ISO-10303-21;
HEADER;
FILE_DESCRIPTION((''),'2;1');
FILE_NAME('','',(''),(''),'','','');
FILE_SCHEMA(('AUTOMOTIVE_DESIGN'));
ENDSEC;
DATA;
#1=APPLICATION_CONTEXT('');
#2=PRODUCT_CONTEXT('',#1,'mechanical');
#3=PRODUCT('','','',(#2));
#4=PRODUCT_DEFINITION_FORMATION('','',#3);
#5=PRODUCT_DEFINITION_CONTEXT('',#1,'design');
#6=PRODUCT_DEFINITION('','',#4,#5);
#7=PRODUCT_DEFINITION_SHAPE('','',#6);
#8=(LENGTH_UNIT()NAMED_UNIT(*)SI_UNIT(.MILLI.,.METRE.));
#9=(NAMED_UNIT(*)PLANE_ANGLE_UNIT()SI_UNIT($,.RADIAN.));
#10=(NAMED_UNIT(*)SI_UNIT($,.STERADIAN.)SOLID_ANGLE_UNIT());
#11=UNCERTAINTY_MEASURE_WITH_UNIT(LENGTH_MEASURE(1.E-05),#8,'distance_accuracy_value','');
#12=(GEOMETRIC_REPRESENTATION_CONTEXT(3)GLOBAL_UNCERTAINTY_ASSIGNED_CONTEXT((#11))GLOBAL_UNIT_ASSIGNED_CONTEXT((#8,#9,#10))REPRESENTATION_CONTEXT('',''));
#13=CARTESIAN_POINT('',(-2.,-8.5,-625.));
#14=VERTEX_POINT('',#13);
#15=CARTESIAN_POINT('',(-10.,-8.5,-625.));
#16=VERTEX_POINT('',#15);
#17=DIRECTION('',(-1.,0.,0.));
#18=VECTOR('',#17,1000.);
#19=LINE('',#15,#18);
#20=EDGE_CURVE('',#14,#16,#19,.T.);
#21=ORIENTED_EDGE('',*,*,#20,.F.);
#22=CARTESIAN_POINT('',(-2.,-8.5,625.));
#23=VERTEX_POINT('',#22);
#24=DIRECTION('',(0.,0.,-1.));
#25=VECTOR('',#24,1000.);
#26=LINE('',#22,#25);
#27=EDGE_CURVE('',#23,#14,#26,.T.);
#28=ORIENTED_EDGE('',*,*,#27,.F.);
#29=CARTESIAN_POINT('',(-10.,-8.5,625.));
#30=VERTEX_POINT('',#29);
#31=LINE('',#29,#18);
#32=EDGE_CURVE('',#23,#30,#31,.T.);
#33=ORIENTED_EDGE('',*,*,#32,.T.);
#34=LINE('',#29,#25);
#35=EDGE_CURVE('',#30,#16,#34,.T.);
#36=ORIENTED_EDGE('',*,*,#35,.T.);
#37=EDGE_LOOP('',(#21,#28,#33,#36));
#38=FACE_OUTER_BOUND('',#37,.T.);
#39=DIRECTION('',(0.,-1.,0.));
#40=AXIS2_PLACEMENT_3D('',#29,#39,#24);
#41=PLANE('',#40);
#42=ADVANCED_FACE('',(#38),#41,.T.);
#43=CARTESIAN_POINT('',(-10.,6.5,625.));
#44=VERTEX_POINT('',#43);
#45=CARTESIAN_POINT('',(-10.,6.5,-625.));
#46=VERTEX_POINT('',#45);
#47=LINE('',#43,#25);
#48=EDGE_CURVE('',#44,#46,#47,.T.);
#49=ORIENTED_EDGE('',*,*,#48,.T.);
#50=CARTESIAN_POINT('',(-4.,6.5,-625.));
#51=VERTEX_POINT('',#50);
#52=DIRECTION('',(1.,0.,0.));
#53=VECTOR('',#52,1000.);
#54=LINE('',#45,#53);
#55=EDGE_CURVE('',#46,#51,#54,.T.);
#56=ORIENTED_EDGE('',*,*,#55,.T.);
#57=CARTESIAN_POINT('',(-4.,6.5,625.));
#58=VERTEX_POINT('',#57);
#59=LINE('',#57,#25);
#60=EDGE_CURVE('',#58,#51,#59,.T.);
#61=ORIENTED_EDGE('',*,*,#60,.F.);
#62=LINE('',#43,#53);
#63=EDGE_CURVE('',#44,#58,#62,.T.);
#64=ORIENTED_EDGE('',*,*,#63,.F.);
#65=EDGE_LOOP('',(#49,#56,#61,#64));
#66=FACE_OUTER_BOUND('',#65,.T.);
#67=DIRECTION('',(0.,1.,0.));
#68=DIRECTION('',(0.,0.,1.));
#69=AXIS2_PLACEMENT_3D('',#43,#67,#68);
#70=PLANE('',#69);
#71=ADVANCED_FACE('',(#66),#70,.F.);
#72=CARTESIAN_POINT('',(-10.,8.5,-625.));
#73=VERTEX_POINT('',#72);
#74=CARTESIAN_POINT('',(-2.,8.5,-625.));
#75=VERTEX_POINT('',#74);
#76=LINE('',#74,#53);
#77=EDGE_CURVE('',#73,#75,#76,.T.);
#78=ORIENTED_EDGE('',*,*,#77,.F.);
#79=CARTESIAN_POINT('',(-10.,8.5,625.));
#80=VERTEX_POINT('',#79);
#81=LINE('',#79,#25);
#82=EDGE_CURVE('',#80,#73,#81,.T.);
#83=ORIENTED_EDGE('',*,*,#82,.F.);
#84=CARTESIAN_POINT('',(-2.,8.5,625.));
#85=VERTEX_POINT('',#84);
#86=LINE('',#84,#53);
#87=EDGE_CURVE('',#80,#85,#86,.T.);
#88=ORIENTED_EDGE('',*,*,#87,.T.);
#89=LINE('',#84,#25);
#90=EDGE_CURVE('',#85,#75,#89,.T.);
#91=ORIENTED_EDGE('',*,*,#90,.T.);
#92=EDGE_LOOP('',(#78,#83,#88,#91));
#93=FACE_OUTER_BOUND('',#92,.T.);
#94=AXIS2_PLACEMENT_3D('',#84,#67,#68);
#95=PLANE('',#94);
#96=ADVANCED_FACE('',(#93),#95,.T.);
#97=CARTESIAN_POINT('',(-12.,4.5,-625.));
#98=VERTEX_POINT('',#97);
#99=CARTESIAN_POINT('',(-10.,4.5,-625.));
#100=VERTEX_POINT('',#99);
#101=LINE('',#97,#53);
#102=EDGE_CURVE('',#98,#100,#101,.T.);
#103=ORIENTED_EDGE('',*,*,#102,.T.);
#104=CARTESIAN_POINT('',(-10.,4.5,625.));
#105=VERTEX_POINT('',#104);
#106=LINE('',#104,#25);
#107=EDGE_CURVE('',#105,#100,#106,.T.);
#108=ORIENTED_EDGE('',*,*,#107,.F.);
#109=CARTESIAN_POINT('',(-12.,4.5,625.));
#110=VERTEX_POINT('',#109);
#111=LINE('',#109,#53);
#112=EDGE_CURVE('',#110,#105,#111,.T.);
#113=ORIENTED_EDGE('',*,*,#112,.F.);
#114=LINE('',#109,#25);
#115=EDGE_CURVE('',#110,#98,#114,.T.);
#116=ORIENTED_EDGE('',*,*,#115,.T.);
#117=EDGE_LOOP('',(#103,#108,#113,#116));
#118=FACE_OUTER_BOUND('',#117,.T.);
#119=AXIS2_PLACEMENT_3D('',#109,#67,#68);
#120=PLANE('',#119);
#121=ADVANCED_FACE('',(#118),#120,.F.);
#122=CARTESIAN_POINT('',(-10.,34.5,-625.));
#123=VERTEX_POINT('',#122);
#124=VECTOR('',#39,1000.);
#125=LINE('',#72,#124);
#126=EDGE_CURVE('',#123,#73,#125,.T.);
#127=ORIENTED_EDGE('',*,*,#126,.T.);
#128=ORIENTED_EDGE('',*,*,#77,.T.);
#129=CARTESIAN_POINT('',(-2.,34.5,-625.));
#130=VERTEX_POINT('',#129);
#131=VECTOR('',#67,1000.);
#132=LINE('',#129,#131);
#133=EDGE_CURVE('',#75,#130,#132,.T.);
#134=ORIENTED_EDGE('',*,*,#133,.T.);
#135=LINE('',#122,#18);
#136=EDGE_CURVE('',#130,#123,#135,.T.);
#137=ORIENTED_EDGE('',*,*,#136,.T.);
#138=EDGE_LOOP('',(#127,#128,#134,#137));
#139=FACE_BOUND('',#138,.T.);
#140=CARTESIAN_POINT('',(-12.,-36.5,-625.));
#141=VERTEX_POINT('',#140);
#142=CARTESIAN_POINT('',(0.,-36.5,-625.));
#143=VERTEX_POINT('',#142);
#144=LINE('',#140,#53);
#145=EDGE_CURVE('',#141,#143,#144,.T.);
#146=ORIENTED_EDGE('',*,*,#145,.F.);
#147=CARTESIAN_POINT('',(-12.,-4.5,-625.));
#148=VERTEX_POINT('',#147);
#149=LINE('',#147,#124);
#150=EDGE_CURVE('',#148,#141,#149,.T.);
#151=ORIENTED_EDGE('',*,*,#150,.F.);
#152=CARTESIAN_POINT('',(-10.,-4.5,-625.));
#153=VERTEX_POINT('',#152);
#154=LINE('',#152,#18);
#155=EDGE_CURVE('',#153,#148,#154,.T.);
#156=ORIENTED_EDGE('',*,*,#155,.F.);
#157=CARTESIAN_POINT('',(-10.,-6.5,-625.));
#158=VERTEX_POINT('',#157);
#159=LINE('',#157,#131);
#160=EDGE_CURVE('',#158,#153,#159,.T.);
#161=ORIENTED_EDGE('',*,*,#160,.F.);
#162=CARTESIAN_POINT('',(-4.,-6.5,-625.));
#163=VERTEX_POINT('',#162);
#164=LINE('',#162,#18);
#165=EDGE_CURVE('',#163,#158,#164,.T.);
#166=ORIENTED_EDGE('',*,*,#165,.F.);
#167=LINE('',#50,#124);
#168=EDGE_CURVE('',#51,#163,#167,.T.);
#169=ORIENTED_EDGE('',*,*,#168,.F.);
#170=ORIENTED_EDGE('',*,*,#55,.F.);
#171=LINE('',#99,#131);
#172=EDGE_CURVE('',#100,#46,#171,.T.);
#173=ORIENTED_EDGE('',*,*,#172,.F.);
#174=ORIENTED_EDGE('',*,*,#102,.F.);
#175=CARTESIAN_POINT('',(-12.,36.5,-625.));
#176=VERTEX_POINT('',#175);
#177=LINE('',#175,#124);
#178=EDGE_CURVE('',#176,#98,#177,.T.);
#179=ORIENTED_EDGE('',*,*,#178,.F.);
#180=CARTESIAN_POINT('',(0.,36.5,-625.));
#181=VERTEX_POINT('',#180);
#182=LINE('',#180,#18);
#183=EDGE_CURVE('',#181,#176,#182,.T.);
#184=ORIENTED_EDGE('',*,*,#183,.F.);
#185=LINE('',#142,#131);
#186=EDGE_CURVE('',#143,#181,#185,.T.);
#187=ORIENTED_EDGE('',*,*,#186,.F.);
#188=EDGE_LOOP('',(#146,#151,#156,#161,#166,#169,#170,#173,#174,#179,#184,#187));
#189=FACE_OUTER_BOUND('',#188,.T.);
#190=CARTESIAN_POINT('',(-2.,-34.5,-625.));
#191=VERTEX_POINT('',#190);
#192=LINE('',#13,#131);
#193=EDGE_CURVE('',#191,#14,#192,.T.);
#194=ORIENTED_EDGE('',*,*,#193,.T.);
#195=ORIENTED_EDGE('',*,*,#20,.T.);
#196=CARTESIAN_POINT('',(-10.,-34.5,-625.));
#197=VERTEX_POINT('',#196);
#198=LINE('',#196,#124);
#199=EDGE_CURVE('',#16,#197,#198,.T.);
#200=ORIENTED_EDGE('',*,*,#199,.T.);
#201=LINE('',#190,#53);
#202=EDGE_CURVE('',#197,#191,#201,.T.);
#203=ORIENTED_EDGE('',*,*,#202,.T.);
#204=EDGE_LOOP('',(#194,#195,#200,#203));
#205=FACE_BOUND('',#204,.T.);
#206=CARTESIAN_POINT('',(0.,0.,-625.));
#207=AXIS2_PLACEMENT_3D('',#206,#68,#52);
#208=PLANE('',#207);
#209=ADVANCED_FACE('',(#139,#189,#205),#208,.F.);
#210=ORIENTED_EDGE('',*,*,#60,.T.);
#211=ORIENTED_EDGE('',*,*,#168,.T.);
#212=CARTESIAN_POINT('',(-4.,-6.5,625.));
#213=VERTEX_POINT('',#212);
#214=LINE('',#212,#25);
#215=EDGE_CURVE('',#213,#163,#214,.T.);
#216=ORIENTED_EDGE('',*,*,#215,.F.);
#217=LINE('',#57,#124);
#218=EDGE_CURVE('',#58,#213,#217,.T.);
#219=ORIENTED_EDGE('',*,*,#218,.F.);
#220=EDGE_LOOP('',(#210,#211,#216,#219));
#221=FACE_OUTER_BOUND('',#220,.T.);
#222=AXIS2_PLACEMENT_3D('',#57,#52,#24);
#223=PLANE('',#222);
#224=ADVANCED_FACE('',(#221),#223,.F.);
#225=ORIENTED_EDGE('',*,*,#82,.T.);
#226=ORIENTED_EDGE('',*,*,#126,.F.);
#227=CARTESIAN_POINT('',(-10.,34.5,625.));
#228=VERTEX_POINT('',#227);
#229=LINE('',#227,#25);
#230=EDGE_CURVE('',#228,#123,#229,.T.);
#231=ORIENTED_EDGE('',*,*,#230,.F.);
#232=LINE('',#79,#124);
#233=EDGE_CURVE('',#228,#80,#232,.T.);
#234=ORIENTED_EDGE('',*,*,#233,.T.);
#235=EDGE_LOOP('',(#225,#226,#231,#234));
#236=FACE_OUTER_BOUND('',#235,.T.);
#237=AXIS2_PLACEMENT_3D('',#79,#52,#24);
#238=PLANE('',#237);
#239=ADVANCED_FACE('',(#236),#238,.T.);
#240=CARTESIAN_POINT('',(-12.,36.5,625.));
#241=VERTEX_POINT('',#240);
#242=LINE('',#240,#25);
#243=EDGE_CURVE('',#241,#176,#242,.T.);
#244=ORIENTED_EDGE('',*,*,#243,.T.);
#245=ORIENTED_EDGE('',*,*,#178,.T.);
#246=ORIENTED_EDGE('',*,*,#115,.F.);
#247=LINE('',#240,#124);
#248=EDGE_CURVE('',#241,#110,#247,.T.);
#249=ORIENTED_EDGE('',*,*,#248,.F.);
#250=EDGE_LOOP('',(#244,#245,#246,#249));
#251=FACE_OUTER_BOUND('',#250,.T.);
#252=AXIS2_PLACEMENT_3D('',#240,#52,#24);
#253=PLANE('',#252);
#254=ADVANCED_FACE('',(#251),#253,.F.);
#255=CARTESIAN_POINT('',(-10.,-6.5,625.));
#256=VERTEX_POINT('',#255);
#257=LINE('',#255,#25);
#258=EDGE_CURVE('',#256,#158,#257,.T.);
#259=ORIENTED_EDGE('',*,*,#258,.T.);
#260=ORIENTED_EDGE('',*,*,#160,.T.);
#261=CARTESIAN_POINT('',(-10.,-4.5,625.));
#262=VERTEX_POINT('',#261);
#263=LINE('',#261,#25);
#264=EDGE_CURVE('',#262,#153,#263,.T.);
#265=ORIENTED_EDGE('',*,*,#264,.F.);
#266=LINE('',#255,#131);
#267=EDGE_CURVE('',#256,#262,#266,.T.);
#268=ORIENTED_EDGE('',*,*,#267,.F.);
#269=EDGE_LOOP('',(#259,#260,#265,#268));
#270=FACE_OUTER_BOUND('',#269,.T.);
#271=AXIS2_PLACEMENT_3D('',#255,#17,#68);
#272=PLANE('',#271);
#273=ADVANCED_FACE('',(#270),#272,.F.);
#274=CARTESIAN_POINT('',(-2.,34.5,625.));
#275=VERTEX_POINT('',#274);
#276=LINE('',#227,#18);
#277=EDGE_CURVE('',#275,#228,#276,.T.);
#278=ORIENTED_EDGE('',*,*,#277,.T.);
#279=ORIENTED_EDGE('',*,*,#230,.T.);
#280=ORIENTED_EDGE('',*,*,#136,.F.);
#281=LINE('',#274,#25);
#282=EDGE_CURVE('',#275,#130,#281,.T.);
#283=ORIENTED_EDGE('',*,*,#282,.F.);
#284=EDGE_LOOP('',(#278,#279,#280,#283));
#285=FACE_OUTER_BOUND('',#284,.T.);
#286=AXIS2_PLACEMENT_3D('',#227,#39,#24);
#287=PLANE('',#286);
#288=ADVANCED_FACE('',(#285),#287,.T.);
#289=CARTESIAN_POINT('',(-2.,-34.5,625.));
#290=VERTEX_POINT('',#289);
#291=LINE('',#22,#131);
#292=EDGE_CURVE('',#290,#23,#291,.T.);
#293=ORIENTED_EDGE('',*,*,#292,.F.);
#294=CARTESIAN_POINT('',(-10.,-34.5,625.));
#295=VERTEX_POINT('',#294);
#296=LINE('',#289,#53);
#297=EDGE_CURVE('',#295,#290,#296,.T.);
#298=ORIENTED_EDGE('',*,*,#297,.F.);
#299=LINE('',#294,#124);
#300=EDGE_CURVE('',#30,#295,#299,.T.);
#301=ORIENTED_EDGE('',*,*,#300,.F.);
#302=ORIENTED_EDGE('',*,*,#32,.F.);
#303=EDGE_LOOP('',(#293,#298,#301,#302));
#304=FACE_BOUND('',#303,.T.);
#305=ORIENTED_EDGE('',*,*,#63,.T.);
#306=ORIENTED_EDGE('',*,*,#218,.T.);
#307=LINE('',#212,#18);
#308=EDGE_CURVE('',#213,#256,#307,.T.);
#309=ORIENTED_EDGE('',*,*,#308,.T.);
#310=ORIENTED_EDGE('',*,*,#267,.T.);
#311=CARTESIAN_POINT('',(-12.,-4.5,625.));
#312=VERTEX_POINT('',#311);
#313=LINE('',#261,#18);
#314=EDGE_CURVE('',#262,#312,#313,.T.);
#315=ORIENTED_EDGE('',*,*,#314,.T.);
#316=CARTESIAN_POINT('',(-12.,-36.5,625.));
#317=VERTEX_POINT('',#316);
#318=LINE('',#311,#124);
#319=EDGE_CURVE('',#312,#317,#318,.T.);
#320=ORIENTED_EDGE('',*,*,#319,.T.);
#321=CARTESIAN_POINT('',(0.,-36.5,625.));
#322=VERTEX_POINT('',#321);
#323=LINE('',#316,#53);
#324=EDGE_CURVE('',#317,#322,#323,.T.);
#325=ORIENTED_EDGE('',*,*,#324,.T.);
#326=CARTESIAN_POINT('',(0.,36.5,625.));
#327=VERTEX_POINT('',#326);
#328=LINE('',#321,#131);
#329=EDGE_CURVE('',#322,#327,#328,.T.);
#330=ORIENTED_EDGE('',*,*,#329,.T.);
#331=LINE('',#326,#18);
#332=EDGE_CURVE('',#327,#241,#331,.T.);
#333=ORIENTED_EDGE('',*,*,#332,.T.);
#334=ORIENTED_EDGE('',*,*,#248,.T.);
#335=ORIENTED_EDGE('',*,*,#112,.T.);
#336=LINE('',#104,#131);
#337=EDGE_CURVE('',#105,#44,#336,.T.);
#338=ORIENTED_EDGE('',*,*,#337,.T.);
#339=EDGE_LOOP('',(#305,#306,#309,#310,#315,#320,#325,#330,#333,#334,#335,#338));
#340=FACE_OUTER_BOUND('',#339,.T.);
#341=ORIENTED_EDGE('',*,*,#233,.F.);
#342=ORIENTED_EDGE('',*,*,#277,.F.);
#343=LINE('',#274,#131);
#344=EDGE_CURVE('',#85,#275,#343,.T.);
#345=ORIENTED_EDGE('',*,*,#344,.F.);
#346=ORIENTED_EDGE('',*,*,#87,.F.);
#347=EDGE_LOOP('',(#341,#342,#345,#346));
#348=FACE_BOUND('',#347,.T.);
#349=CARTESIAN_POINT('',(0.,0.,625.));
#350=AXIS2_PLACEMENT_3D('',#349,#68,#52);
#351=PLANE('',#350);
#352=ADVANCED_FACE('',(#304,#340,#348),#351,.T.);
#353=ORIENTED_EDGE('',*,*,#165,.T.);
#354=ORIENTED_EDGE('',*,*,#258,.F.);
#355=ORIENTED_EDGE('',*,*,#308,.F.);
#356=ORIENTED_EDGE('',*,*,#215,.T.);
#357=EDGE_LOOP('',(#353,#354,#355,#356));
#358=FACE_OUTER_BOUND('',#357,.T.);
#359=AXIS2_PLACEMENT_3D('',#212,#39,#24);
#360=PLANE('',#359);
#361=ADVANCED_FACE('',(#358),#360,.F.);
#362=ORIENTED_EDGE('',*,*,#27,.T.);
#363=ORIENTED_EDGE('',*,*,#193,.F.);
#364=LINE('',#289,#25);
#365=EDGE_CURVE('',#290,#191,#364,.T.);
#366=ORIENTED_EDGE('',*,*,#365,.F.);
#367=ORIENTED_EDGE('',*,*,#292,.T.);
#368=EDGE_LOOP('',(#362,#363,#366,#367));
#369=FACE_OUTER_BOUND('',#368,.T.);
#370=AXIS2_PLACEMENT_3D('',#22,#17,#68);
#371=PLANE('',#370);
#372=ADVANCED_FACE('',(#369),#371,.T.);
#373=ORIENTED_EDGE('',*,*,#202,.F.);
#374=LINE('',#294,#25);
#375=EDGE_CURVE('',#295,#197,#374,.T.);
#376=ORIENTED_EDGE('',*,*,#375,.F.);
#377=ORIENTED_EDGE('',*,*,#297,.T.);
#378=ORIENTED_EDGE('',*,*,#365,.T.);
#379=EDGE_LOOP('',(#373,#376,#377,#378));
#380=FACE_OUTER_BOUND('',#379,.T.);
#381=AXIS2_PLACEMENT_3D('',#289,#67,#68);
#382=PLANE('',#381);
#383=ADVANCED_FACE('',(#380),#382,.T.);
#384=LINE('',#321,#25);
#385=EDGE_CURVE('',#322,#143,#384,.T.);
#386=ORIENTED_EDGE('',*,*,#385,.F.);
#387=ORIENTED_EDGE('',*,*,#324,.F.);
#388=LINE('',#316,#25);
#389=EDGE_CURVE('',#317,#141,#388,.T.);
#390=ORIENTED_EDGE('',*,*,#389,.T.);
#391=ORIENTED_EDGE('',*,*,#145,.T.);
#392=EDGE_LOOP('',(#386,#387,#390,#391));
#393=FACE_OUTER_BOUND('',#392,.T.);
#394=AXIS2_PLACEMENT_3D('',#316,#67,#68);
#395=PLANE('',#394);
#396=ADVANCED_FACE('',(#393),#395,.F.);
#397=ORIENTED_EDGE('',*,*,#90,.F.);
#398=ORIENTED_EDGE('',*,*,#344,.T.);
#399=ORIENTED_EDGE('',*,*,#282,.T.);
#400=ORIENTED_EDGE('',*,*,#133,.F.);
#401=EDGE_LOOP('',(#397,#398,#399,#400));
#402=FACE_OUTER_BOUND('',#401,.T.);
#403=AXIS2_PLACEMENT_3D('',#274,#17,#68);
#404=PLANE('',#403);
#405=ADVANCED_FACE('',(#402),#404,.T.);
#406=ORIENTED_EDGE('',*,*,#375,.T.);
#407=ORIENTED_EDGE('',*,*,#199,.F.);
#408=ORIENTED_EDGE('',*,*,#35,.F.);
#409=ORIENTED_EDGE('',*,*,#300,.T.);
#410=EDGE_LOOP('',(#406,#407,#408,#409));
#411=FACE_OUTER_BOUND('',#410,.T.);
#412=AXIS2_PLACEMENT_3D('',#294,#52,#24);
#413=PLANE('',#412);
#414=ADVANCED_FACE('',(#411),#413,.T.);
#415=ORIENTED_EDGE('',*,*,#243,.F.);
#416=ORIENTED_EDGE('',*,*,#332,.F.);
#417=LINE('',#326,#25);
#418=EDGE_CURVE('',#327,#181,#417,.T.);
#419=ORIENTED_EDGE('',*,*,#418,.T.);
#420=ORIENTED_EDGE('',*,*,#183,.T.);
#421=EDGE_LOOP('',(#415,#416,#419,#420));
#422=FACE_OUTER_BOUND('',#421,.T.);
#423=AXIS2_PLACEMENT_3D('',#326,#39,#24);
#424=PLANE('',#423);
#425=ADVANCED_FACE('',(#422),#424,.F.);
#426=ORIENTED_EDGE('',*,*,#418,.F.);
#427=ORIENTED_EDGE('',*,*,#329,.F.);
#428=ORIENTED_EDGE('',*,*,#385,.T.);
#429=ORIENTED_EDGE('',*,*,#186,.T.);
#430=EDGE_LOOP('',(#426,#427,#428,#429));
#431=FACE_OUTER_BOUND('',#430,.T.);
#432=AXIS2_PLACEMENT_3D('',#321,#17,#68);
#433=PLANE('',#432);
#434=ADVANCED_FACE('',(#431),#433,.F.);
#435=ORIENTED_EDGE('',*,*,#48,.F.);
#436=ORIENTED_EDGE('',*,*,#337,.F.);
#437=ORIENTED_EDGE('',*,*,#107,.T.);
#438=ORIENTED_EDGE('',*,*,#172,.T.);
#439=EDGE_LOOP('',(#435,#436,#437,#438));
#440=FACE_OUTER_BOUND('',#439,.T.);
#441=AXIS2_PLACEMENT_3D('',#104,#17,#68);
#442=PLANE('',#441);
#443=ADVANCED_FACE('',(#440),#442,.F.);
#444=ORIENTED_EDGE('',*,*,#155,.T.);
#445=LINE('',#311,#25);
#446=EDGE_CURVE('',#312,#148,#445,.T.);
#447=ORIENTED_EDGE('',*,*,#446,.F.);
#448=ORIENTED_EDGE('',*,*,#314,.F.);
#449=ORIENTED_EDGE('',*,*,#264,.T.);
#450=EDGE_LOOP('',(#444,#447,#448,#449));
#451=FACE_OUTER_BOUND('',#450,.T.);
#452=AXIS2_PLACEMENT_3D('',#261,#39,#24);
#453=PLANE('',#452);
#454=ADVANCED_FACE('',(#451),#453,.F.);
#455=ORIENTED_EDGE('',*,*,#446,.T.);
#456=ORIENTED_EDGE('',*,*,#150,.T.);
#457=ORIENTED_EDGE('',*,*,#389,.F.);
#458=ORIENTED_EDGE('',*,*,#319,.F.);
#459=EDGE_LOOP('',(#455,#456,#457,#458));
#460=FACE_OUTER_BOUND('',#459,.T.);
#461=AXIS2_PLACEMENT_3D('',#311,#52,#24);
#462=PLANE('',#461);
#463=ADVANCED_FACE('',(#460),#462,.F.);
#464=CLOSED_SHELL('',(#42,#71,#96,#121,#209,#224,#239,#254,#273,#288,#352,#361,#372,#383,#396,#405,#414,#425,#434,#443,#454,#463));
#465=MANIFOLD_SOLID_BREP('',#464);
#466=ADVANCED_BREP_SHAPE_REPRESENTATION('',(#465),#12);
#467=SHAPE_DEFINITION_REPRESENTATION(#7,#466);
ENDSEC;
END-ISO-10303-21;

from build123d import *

# Parameters (mm, degrees)
SKETCH_1_W      = 8
SKETCH_1_H      = 26
EXTRUDE_1_DEPTH = 625


with BuildPart() as part:
    # 草图1 → 凸台-拉伸1 (new, symmetric)
    with BuildSketch(Plane.XY):
        Polygon((-12, 4.5), (-10, 4.5), (-10, 6.5), (-4, 6.5), (-4, -6.5), (-10, -6.5), (-10, -4.5), (-12, -4.5), (-12, -36.5), (0, -36.5), (0, 36.5), (-12, 36.5), align=None)
        with Locations((-6, -21.5)):
            Rectangle(SKETCH_1_W, SKETCH_1_H, mode=Mode.SUBTRACT)
        with Locations((-6, 21.5)):
            Rectangle(SKETCH_1_W, SKETCH_1_H, mode=Mode.SUBTRACT)
    extrude(amount=EXTRUDE_1_DEPTH, both=True)


solid = part.part
